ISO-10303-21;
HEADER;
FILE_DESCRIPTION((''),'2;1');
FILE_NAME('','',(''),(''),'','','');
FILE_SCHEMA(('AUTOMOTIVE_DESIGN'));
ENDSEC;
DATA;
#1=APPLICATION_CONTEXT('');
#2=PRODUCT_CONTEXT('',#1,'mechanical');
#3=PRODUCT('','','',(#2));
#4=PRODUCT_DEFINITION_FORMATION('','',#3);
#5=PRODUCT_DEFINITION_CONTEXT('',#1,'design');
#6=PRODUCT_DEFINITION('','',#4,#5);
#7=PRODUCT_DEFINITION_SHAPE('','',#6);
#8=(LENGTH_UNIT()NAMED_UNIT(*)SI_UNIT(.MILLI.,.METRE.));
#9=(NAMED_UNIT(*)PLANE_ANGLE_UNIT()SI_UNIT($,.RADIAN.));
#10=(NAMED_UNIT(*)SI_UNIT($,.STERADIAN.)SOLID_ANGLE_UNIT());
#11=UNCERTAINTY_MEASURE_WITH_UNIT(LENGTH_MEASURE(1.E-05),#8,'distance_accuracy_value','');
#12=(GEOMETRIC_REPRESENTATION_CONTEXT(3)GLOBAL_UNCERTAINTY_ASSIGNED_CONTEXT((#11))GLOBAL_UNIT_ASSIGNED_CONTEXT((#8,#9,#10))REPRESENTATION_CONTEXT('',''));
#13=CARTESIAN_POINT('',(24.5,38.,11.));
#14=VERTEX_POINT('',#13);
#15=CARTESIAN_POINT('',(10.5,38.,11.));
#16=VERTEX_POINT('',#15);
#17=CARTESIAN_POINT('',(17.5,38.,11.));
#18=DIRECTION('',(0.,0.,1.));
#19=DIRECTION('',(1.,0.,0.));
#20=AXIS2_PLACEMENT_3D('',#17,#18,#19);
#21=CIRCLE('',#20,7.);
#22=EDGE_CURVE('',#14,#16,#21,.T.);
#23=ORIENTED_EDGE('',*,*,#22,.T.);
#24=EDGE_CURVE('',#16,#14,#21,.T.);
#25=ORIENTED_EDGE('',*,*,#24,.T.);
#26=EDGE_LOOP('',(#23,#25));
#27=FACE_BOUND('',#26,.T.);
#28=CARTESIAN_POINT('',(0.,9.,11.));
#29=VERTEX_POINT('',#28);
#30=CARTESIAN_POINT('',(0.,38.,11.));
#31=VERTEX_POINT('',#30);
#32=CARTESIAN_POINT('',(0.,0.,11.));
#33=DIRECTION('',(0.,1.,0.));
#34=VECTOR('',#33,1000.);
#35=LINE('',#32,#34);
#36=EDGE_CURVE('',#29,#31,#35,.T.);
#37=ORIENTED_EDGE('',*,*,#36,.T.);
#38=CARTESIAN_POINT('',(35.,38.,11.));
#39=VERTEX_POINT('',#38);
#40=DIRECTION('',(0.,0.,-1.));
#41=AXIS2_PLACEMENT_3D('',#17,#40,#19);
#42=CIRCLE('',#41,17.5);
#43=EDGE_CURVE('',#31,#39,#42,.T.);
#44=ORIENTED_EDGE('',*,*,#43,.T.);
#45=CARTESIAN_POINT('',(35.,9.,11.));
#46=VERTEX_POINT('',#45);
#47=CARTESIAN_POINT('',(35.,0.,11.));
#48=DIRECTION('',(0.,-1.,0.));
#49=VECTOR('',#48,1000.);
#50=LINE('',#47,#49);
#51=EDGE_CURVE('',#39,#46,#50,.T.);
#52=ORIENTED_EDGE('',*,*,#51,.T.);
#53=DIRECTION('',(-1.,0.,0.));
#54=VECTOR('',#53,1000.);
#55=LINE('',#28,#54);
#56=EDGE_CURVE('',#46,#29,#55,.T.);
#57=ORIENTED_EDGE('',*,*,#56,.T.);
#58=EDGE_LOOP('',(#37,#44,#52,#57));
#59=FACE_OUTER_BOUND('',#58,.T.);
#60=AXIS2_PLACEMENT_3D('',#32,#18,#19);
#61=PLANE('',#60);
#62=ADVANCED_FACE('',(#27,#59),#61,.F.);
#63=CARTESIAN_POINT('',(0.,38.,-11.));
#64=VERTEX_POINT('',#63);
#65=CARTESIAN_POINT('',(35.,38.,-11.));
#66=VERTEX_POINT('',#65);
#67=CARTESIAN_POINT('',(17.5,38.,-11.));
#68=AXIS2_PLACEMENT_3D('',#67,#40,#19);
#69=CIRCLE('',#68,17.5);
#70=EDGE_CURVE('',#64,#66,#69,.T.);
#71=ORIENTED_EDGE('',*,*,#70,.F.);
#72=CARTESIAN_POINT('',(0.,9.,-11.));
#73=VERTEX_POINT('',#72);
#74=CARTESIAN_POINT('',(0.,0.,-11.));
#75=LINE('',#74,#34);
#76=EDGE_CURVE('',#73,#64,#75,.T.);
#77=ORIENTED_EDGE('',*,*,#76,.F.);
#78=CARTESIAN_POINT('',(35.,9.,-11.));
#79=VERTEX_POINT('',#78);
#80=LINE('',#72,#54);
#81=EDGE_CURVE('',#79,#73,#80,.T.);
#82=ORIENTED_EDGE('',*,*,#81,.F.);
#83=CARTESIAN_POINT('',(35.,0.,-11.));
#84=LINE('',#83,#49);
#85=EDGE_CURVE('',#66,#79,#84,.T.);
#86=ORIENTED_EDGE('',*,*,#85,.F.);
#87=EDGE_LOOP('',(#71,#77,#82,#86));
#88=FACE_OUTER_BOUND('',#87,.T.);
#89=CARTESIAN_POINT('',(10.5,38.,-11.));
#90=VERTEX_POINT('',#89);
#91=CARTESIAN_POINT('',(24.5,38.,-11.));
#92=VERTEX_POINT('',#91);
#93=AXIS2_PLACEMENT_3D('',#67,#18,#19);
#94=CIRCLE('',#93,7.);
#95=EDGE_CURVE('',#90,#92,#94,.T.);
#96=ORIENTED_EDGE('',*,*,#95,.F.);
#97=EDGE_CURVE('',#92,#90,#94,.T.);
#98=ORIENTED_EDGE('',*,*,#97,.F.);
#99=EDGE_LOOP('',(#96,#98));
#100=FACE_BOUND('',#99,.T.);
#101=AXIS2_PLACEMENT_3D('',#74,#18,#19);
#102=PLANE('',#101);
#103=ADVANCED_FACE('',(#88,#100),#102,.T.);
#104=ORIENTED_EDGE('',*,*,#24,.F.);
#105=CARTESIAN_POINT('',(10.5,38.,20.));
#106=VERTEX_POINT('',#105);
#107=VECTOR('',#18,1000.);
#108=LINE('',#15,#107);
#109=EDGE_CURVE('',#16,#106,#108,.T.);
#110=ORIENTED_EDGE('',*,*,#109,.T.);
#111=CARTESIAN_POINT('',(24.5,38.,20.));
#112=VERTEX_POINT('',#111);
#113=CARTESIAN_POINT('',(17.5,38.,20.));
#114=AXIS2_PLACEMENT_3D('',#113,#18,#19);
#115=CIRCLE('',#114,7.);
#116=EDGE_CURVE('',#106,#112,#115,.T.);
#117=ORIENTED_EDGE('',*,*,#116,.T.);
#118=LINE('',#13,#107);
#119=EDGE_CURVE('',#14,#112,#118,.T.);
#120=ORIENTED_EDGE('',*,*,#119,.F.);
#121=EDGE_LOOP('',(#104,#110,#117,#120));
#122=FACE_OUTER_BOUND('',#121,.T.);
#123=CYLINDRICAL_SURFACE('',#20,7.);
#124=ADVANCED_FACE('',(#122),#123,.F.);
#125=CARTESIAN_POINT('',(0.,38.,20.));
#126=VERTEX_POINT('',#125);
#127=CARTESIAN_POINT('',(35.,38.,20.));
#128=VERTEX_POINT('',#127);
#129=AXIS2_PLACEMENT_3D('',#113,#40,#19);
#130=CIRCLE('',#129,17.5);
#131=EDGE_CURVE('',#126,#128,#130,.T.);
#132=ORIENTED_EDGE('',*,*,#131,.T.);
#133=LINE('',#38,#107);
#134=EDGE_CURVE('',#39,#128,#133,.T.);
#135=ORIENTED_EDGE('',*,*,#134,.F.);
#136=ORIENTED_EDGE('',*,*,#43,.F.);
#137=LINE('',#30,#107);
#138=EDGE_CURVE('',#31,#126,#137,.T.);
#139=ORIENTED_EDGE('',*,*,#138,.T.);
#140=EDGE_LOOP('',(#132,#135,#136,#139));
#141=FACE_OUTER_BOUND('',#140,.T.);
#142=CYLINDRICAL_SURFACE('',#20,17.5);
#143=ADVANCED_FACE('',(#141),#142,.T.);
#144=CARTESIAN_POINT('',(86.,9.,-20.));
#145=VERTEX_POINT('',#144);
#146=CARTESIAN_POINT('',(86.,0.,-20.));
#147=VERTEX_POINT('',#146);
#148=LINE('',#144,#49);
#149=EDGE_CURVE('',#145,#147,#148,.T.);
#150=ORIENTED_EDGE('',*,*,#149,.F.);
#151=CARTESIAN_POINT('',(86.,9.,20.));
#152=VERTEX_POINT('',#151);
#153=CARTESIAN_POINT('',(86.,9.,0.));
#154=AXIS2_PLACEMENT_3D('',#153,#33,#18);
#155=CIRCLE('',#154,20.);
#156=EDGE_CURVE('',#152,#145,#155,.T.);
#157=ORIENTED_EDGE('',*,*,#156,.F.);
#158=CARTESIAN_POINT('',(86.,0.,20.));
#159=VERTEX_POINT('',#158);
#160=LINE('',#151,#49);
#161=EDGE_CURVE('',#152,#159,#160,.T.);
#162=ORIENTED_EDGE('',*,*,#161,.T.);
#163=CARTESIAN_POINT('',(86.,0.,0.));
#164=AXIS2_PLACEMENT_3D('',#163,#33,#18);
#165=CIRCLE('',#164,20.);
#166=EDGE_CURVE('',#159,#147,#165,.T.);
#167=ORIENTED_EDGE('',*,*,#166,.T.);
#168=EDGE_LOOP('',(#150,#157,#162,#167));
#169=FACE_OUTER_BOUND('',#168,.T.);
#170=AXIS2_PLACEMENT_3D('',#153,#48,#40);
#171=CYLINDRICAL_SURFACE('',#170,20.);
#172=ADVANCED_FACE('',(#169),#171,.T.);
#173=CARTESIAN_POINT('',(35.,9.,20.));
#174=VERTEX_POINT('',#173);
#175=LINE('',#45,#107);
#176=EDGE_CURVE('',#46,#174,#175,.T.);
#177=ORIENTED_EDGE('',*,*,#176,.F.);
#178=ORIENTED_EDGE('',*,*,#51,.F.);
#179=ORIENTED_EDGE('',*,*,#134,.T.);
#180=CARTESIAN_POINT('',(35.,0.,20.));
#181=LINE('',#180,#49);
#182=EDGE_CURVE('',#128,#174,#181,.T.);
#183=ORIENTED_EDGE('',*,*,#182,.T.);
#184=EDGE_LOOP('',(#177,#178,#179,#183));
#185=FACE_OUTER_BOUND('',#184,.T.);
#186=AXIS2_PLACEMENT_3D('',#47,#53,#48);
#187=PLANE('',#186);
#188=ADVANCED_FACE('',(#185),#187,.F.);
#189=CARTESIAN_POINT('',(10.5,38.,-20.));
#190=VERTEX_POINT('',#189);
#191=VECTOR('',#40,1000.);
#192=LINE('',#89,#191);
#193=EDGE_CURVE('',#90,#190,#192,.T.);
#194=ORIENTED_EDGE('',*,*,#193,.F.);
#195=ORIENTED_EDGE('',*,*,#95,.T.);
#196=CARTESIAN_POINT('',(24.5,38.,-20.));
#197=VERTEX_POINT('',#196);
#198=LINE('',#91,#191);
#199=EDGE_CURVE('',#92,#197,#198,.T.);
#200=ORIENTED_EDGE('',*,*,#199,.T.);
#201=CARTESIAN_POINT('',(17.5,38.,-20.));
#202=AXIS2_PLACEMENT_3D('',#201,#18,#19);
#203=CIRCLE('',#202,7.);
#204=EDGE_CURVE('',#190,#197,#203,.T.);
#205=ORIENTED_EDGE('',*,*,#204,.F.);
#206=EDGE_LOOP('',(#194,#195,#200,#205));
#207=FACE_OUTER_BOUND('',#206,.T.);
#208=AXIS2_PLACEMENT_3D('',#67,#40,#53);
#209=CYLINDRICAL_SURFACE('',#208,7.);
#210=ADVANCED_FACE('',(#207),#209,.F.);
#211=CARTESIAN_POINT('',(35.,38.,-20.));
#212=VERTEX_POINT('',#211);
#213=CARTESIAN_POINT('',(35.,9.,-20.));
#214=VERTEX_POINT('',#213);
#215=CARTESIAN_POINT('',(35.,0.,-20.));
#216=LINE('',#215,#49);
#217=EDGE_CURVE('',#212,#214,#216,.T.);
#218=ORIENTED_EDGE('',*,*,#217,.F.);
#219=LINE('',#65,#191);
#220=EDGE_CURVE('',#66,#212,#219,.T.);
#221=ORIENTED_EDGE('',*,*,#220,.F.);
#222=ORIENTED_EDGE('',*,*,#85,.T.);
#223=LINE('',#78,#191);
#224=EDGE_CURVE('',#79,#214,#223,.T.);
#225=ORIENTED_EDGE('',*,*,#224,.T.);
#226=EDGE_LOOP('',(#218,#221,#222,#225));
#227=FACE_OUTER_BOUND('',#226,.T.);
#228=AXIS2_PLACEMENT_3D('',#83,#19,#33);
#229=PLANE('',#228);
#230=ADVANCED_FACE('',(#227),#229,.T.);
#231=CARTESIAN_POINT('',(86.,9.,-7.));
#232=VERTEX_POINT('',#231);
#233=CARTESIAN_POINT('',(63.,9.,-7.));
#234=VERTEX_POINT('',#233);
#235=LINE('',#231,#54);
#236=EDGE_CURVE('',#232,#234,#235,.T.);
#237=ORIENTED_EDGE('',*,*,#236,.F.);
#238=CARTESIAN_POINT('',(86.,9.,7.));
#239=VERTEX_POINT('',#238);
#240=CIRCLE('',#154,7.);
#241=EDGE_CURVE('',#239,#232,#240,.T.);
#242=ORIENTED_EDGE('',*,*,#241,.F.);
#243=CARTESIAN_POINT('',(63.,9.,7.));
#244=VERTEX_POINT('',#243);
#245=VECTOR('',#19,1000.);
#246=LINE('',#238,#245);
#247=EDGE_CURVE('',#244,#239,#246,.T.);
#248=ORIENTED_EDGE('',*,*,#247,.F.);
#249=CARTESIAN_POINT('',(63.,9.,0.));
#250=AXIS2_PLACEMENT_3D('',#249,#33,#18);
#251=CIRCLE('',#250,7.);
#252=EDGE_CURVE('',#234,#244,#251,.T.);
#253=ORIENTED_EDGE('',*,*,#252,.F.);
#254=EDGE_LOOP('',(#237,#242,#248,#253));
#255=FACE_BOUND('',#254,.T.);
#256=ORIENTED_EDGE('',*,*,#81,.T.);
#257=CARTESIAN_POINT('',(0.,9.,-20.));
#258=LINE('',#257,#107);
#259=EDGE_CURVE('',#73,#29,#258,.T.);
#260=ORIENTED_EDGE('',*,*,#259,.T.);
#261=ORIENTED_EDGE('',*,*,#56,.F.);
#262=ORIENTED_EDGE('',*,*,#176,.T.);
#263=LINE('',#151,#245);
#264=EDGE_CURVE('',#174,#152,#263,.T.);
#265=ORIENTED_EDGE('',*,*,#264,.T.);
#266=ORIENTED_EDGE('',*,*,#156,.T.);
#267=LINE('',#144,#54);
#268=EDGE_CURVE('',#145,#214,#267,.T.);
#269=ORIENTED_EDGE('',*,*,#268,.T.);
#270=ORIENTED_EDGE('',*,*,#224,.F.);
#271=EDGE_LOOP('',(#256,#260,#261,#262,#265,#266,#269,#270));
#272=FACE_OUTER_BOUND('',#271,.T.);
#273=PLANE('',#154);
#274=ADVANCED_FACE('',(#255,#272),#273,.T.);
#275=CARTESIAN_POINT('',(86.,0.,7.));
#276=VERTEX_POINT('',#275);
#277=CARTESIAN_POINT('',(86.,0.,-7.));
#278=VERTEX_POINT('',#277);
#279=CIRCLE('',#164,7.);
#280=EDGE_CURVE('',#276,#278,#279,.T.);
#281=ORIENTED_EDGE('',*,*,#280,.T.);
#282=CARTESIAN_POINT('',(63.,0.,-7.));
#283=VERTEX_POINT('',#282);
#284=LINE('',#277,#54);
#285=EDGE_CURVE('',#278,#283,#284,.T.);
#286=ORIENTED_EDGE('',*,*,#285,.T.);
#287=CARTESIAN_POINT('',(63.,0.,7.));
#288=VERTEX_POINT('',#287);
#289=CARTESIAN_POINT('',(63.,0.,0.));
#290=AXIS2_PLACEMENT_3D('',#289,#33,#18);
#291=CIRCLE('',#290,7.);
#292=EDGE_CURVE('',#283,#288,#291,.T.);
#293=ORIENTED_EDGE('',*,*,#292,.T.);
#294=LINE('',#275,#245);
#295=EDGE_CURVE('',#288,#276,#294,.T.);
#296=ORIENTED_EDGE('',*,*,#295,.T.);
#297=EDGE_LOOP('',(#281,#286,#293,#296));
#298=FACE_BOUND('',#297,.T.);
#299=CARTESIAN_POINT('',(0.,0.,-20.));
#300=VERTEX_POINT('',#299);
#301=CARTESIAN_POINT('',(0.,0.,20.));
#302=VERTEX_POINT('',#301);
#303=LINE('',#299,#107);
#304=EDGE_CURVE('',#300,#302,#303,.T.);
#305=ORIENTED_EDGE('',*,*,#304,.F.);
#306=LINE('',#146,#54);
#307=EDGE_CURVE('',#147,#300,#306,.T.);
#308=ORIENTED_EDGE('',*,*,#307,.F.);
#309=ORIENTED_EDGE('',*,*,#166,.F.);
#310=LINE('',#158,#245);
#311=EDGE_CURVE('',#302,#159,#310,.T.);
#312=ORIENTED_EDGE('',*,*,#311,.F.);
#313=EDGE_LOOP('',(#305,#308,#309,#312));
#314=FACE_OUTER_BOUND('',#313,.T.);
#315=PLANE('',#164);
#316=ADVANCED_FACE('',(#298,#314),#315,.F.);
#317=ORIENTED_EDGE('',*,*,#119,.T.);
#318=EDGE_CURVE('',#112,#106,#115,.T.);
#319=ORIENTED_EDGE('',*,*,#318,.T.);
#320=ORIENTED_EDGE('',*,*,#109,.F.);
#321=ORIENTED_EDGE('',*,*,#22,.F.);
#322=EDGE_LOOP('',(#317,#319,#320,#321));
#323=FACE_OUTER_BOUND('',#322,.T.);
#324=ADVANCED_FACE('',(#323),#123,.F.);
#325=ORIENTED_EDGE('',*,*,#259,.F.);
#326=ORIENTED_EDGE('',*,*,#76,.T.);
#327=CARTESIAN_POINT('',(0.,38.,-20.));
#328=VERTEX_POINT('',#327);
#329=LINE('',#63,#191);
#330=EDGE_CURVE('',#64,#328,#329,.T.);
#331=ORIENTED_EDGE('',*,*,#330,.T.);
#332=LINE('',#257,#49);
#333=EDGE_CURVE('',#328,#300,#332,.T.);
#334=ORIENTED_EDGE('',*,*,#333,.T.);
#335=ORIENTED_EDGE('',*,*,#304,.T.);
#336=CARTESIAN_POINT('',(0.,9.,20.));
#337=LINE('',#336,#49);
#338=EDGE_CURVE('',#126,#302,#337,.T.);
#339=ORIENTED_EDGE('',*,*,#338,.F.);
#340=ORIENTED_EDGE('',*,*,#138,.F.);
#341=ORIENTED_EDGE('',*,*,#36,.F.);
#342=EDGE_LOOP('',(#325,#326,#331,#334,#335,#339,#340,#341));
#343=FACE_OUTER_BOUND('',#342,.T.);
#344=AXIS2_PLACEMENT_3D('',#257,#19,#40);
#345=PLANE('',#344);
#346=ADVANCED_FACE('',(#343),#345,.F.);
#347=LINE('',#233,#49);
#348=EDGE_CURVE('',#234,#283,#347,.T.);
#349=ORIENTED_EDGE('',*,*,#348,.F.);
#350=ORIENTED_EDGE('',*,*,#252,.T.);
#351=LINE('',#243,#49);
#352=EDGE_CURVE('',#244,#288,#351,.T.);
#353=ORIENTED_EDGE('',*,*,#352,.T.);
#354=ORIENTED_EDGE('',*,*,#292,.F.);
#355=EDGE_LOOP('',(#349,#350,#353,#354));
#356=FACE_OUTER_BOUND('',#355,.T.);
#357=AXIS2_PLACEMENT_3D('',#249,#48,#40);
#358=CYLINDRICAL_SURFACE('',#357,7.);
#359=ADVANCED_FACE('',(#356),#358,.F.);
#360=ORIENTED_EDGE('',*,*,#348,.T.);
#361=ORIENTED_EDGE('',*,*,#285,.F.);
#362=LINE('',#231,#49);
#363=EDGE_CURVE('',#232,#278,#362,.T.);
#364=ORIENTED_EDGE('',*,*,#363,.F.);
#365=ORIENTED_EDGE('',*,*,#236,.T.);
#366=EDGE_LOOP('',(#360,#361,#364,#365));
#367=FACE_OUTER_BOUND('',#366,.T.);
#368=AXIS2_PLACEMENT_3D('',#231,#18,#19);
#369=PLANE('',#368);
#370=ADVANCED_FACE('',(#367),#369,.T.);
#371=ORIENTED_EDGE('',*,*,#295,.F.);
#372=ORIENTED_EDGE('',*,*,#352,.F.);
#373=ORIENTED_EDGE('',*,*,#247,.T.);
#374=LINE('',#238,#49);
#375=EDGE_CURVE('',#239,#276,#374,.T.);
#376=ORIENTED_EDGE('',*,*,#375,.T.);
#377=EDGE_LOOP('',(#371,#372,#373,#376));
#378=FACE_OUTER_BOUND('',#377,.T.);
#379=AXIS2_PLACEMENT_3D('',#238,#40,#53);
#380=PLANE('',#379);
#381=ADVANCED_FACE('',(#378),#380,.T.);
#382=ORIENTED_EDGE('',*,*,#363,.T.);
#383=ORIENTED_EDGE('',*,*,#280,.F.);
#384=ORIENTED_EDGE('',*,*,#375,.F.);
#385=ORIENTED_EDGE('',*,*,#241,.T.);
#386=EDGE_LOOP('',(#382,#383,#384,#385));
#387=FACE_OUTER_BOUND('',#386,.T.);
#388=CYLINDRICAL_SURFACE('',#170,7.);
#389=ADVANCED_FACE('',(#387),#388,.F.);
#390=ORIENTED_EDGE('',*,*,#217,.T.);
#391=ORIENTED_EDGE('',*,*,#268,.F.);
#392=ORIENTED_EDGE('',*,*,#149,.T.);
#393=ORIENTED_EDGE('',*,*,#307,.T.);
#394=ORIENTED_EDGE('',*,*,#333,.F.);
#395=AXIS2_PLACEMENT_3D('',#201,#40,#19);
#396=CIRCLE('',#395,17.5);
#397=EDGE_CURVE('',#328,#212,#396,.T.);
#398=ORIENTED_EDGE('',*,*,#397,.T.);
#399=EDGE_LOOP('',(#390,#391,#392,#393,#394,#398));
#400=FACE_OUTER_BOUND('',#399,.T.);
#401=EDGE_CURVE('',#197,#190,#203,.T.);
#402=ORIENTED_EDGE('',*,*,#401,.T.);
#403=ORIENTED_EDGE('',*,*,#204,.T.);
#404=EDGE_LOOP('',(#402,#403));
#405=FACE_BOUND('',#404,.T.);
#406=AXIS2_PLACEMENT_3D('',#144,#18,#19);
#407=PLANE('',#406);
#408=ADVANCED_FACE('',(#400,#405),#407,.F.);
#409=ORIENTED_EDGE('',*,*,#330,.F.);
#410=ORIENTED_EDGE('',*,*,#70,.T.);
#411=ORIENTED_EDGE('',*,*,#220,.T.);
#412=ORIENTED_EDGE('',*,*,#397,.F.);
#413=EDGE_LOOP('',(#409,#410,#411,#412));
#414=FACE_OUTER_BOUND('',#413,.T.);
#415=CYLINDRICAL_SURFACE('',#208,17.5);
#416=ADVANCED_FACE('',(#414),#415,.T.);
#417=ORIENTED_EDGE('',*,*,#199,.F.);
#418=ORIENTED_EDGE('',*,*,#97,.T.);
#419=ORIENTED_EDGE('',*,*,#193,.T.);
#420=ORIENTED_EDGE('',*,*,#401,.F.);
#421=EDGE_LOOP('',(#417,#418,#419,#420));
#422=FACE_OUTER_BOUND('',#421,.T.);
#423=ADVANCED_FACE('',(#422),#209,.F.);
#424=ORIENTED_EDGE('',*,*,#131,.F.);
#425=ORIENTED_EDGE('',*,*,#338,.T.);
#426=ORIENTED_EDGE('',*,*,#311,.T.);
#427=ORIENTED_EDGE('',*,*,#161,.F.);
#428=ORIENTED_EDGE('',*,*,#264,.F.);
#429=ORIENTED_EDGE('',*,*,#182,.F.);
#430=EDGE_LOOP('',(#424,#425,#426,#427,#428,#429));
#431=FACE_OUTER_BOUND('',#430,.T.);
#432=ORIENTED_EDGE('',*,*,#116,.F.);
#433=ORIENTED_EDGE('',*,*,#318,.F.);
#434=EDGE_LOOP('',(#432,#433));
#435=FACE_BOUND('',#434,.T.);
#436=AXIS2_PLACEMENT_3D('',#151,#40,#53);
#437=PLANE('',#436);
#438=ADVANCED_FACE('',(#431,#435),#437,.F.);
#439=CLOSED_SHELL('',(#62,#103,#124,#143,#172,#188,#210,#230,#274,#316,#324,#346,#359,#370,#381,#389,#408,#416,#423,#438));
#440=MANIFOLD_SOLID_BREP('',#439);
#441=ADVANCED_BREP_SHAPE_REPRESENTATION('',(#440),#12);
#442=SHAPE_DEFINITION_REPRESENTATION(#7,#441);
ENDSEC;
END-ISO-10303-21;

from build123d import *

# Parameters (mm, degrees)
SLOTTED_BASE_PLATE_DEPTH    = 9
CLEVIS_EAR_PROFILE_SKETCH_R = 7
CLEVIS_EAR_1_DEPTH          = 9
CLEVIS_START                = -31
SKETCH3_3_R                 = 7
CLEVIS_EAR_2_DEPTH          = 9


with BuildPart() as part:
    # Base Plate Slot Profile Sketch → Slotted Base Plate (new body)
    with BuildSketch(Plane(origin=(0, 0, 0), x_dir=(1, 0, 0), z_dir=(0, 1, 0))):
        with BuildLine():
            Line((0, 20), (0, -20))
            Line((0, -20), (86, -20))
            ThreePointArc((86, -20), (106, 0), (86, 20))
            Line((86, 20), (0, 20))
        make_face()
        with BuildLine():
            Line((86, -7), (63, -7))
            ThreePointArc((63, -7), (56, 0), (63, 7))
            Line((63, 7), (86, 7))
            ThreePointArc((86, 7), (93, 0), (86, -7))
        make_face(mode=Mode.SUBTRACT)
    extrude(amount=SLOTTED_BASE_PLATE_DEPTH)

    # Clevis Ear Profile Sketch → Clevis Ear 1 (add)
    with BuildSketch(Plane.XY.offset(20)):
        with BuildLine():
            Line((0, 38), (0, 9))
            Line((0, 9), (35, 9))
            Line((35, 9), (35, 38))
            ThreePointArc((35, 38), (17.5, 55.5), (0, 38))
        make_face()
        with Locations((17.5, 38)):
            Circle(CLEVIS_EAR_PROFILE_SKETCH_R, mode=Mode.SUBTRACT)
    extrude(amount=-CLEVIS_EAR_1_DEPTH)

    # Sketch3_3 → Clevis Ear 2 (add)
    with BuildSketch(Plane.XY.offset(20).offset(CLEVIS_START)):
        with BuildLine():
            Line((0, 38), (0, 9))
            Line((0, 9), (0, 0))
            Line((0, 0), (86, 0))
            Line((86, 0), (86, 9))
            Line((86, 9), (35, 9))
            Line((35, 9), (35, 38))
            ThreePointArc((35, 38), (17.5, 55.5), (0, 38))
        make_face()
        with Locations((17.5, 38)):
            Circle(SKETCH3_3_R, mode=Mode.SUBTRACT)
    extrude(amount=-CLEVIS_EAR_2_DEPTH)


solid = part.part
